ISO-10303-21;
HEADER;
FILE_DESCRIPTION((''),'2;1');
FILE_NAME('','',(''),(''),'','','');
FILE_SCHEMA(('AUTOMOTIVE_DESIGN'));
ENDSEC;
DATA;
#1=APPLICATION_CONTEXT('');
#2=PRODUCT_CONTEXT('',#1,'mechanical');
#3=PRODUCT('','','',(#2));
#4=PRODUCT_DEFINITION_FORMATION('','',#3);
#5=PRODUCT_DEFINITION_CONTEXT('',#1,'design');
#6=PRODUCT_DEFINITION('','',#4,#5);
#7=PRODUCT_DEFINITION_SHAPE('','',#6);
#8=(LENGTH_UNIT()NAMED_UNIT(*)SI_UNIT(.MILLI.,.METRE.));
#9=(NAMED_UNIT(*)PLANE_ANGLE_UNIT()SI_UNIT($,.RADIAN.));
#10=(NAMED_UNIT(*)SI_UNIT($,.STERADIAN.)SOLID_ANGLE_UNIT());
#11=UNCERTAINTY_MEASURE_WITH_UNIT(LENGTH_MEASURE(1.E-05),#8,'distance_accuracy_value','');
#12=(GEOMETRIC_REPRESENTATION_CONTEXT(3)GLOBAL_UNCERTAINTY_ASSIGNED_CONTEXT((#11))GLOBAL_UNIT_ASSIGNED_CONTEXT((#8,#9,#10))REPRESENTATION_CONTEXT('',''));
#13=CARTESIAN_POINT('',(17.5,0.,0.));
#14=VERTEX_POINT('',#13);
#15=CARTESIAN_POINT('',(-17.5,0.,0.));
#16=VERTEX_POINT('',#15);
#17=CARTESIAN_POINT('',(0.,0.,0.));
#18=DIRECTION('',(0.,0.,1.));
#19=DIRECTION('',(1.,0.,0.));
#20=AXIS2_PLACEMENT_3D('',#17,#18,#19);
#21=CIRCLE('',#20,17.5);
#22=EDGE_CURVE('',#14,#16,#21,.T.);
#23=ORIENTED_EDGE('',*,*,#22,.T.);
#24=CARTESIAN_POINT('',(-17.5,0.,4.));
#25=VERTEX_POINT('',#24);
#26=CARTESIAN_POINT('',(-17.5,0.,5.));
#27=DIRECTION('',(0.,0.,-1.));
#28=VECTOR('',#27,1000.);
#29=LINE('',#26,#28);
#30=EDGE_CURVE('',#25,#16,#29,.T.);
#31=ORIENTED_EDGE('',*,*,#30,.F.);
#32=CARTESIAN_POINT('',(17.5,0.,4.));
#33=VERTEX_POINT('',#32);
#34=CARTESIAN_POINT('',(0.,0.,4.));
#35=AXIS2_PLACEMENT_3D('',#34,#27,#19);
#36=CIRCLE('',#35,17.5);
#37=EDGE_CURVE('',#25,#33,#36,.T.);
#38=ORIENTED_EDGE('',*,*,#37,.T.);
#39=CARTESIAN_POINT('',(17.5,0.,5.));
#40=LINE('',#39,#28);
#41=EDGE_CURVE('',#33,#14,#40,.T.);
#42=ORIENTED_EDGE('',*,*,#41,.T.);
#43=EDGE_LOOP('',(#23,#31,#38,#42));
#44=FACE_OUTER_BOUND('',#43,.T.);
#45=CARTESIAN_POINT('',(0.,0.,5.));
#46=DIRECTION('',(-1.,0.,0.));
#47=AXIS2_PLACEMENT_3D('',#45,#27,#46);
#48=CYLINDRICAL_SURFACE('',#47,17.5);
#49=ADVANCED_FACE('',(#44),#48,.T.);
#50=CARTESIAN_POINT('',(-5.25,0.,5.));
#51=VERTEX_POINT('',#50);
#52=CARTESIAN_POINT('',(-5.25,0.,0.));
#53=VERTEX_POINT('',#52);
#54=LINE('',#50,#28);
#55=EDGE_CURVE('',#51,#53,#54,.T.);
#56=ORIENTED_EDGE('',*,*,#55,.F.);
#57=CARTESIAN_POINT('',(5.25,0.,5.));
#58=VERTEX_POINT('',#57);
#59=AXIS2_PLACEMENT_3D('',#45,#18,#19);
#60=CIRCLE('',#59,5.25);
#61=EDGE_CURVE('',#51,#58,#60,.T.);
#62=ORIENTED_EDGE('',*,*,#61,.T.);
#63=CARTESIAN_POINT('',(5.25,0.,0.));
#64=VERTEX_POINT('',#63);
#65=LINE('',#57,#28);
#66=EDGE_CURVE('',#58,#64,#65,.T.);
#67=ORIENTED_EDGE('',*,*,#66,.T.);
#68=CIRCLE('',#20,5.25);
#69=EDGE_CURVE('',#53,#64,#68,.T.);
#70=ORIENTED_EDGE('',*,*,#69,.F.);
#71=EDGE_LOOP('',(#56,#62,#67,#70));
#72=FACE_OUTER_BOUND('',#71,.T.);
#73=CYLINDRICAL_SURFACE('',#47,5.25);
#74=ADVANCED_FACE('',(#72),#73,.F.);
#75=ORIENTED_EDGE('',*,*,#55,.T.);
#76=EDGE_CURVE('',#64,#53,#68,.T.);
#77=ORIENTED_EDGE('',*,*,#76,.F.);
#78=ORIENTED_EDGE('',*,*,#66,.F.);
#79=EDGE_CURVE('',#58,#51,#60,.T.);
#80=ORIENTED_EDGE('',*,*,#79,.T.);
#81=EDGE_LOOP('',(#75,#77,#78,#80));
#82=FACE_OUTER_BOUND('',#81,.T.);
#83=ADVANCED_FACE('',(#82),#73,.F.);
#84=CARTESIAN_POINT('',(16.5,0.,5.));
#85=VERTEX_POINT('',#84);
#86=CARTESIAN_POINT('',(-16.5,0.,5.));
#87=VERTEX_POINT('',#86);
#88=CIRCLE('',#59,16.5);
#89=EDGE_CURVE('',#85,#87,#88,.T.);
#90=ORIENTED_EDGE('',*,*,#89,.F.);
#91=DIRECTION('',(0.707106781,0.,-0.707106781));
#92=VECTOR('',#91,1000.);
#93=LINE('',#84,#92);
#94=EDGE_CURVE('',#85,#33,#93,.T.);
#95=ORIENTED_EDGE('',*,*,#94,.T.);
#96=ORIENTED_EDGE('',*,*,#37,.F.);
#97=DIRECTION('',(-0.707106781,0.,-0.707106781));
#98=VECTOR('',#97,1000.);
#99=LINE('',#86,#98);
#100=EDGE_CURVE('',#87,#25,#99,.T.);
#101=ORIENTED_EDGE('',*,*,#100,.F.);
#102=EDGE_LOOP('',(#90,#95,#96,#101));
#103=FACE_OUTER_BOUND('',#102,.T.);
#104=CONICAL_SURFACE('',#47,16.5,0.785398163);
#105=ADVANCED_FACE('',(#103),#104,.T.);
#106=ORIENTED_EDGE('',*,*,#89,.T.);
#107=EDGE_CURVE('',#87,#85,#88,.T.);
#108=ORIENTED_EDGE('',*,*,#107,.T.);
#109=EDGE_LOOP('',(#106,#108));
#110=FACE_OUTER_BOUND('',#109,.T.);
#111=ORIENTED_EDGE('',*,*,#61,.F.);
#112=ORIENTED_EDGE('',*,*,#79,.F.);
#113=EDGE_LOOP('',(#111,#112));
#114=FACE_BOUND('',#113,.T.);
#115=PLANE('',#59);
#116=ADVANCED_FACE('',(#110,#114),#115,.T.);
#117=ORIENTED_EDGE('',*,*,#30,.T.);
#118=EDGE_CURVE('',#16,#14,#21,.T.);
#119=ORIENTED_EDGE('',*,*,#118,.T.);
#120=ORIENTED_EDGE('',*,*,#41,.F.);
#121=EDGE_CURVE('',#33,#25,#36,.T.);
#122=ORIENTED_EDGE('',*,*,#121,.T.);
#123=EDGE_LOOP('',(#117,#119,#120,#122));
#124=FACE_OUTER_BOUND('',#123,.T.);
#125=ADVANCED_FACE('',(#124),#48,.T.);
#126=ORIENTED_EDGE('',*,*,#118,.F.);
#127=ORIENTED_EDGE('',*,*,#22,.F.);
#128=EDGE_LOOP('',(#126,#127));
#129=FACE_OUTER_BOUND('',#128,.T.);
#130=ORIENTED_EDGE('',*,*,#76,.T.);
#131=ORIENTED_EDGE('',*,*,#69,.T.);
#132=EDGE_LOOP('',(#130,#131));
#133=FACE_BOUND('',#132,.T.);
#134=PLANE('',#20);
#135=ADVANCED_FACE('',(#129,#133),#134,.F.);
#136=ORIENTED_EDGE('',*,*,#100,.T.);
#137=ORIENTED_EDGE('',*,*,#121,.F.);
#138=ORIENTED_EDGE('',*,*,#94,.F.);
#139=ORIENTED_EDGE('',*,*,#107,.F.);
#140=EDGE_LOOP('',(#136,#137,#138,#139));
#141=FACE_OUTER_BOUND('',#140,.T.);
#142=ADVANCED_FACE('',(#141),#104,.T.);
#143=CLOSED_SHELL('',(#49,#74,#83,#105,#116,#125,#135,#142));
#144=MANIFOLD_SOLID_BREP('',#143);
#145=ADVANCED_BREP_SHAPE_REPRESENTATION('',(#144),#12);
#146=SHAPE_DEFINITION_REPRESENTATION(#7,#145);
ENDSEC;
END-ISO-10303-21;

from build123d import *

# Parameters (mm, degrees)
SKETCH_1_R      = 17.5
SKETCH_1_R_2    = 5.25
EXTRUDE_1_DEPTH = 5
CHAMFER_1_SIZE  = 1


with BuildPart() as part:
    # 草图1 → 凸台-拉伸1 (new body)
    with BuildSketch(Plane.XY):
        Circle(SKETCH_1_R)
        Circle(SKETCH_1_R_2, mode=Mode.SUBTRACT)
    extrude(amount=EXTRUDE_1_DEPTH)

    # 倒角1
    chamfer_1_edges = [part.edges().sort_by_distance(p)[0] for p in [
        (-17.5, 0, 5),
    ]]
    chamfer(chamfer_1_edges, length=CHAMFER_1_SIZE)


solid = part.part
